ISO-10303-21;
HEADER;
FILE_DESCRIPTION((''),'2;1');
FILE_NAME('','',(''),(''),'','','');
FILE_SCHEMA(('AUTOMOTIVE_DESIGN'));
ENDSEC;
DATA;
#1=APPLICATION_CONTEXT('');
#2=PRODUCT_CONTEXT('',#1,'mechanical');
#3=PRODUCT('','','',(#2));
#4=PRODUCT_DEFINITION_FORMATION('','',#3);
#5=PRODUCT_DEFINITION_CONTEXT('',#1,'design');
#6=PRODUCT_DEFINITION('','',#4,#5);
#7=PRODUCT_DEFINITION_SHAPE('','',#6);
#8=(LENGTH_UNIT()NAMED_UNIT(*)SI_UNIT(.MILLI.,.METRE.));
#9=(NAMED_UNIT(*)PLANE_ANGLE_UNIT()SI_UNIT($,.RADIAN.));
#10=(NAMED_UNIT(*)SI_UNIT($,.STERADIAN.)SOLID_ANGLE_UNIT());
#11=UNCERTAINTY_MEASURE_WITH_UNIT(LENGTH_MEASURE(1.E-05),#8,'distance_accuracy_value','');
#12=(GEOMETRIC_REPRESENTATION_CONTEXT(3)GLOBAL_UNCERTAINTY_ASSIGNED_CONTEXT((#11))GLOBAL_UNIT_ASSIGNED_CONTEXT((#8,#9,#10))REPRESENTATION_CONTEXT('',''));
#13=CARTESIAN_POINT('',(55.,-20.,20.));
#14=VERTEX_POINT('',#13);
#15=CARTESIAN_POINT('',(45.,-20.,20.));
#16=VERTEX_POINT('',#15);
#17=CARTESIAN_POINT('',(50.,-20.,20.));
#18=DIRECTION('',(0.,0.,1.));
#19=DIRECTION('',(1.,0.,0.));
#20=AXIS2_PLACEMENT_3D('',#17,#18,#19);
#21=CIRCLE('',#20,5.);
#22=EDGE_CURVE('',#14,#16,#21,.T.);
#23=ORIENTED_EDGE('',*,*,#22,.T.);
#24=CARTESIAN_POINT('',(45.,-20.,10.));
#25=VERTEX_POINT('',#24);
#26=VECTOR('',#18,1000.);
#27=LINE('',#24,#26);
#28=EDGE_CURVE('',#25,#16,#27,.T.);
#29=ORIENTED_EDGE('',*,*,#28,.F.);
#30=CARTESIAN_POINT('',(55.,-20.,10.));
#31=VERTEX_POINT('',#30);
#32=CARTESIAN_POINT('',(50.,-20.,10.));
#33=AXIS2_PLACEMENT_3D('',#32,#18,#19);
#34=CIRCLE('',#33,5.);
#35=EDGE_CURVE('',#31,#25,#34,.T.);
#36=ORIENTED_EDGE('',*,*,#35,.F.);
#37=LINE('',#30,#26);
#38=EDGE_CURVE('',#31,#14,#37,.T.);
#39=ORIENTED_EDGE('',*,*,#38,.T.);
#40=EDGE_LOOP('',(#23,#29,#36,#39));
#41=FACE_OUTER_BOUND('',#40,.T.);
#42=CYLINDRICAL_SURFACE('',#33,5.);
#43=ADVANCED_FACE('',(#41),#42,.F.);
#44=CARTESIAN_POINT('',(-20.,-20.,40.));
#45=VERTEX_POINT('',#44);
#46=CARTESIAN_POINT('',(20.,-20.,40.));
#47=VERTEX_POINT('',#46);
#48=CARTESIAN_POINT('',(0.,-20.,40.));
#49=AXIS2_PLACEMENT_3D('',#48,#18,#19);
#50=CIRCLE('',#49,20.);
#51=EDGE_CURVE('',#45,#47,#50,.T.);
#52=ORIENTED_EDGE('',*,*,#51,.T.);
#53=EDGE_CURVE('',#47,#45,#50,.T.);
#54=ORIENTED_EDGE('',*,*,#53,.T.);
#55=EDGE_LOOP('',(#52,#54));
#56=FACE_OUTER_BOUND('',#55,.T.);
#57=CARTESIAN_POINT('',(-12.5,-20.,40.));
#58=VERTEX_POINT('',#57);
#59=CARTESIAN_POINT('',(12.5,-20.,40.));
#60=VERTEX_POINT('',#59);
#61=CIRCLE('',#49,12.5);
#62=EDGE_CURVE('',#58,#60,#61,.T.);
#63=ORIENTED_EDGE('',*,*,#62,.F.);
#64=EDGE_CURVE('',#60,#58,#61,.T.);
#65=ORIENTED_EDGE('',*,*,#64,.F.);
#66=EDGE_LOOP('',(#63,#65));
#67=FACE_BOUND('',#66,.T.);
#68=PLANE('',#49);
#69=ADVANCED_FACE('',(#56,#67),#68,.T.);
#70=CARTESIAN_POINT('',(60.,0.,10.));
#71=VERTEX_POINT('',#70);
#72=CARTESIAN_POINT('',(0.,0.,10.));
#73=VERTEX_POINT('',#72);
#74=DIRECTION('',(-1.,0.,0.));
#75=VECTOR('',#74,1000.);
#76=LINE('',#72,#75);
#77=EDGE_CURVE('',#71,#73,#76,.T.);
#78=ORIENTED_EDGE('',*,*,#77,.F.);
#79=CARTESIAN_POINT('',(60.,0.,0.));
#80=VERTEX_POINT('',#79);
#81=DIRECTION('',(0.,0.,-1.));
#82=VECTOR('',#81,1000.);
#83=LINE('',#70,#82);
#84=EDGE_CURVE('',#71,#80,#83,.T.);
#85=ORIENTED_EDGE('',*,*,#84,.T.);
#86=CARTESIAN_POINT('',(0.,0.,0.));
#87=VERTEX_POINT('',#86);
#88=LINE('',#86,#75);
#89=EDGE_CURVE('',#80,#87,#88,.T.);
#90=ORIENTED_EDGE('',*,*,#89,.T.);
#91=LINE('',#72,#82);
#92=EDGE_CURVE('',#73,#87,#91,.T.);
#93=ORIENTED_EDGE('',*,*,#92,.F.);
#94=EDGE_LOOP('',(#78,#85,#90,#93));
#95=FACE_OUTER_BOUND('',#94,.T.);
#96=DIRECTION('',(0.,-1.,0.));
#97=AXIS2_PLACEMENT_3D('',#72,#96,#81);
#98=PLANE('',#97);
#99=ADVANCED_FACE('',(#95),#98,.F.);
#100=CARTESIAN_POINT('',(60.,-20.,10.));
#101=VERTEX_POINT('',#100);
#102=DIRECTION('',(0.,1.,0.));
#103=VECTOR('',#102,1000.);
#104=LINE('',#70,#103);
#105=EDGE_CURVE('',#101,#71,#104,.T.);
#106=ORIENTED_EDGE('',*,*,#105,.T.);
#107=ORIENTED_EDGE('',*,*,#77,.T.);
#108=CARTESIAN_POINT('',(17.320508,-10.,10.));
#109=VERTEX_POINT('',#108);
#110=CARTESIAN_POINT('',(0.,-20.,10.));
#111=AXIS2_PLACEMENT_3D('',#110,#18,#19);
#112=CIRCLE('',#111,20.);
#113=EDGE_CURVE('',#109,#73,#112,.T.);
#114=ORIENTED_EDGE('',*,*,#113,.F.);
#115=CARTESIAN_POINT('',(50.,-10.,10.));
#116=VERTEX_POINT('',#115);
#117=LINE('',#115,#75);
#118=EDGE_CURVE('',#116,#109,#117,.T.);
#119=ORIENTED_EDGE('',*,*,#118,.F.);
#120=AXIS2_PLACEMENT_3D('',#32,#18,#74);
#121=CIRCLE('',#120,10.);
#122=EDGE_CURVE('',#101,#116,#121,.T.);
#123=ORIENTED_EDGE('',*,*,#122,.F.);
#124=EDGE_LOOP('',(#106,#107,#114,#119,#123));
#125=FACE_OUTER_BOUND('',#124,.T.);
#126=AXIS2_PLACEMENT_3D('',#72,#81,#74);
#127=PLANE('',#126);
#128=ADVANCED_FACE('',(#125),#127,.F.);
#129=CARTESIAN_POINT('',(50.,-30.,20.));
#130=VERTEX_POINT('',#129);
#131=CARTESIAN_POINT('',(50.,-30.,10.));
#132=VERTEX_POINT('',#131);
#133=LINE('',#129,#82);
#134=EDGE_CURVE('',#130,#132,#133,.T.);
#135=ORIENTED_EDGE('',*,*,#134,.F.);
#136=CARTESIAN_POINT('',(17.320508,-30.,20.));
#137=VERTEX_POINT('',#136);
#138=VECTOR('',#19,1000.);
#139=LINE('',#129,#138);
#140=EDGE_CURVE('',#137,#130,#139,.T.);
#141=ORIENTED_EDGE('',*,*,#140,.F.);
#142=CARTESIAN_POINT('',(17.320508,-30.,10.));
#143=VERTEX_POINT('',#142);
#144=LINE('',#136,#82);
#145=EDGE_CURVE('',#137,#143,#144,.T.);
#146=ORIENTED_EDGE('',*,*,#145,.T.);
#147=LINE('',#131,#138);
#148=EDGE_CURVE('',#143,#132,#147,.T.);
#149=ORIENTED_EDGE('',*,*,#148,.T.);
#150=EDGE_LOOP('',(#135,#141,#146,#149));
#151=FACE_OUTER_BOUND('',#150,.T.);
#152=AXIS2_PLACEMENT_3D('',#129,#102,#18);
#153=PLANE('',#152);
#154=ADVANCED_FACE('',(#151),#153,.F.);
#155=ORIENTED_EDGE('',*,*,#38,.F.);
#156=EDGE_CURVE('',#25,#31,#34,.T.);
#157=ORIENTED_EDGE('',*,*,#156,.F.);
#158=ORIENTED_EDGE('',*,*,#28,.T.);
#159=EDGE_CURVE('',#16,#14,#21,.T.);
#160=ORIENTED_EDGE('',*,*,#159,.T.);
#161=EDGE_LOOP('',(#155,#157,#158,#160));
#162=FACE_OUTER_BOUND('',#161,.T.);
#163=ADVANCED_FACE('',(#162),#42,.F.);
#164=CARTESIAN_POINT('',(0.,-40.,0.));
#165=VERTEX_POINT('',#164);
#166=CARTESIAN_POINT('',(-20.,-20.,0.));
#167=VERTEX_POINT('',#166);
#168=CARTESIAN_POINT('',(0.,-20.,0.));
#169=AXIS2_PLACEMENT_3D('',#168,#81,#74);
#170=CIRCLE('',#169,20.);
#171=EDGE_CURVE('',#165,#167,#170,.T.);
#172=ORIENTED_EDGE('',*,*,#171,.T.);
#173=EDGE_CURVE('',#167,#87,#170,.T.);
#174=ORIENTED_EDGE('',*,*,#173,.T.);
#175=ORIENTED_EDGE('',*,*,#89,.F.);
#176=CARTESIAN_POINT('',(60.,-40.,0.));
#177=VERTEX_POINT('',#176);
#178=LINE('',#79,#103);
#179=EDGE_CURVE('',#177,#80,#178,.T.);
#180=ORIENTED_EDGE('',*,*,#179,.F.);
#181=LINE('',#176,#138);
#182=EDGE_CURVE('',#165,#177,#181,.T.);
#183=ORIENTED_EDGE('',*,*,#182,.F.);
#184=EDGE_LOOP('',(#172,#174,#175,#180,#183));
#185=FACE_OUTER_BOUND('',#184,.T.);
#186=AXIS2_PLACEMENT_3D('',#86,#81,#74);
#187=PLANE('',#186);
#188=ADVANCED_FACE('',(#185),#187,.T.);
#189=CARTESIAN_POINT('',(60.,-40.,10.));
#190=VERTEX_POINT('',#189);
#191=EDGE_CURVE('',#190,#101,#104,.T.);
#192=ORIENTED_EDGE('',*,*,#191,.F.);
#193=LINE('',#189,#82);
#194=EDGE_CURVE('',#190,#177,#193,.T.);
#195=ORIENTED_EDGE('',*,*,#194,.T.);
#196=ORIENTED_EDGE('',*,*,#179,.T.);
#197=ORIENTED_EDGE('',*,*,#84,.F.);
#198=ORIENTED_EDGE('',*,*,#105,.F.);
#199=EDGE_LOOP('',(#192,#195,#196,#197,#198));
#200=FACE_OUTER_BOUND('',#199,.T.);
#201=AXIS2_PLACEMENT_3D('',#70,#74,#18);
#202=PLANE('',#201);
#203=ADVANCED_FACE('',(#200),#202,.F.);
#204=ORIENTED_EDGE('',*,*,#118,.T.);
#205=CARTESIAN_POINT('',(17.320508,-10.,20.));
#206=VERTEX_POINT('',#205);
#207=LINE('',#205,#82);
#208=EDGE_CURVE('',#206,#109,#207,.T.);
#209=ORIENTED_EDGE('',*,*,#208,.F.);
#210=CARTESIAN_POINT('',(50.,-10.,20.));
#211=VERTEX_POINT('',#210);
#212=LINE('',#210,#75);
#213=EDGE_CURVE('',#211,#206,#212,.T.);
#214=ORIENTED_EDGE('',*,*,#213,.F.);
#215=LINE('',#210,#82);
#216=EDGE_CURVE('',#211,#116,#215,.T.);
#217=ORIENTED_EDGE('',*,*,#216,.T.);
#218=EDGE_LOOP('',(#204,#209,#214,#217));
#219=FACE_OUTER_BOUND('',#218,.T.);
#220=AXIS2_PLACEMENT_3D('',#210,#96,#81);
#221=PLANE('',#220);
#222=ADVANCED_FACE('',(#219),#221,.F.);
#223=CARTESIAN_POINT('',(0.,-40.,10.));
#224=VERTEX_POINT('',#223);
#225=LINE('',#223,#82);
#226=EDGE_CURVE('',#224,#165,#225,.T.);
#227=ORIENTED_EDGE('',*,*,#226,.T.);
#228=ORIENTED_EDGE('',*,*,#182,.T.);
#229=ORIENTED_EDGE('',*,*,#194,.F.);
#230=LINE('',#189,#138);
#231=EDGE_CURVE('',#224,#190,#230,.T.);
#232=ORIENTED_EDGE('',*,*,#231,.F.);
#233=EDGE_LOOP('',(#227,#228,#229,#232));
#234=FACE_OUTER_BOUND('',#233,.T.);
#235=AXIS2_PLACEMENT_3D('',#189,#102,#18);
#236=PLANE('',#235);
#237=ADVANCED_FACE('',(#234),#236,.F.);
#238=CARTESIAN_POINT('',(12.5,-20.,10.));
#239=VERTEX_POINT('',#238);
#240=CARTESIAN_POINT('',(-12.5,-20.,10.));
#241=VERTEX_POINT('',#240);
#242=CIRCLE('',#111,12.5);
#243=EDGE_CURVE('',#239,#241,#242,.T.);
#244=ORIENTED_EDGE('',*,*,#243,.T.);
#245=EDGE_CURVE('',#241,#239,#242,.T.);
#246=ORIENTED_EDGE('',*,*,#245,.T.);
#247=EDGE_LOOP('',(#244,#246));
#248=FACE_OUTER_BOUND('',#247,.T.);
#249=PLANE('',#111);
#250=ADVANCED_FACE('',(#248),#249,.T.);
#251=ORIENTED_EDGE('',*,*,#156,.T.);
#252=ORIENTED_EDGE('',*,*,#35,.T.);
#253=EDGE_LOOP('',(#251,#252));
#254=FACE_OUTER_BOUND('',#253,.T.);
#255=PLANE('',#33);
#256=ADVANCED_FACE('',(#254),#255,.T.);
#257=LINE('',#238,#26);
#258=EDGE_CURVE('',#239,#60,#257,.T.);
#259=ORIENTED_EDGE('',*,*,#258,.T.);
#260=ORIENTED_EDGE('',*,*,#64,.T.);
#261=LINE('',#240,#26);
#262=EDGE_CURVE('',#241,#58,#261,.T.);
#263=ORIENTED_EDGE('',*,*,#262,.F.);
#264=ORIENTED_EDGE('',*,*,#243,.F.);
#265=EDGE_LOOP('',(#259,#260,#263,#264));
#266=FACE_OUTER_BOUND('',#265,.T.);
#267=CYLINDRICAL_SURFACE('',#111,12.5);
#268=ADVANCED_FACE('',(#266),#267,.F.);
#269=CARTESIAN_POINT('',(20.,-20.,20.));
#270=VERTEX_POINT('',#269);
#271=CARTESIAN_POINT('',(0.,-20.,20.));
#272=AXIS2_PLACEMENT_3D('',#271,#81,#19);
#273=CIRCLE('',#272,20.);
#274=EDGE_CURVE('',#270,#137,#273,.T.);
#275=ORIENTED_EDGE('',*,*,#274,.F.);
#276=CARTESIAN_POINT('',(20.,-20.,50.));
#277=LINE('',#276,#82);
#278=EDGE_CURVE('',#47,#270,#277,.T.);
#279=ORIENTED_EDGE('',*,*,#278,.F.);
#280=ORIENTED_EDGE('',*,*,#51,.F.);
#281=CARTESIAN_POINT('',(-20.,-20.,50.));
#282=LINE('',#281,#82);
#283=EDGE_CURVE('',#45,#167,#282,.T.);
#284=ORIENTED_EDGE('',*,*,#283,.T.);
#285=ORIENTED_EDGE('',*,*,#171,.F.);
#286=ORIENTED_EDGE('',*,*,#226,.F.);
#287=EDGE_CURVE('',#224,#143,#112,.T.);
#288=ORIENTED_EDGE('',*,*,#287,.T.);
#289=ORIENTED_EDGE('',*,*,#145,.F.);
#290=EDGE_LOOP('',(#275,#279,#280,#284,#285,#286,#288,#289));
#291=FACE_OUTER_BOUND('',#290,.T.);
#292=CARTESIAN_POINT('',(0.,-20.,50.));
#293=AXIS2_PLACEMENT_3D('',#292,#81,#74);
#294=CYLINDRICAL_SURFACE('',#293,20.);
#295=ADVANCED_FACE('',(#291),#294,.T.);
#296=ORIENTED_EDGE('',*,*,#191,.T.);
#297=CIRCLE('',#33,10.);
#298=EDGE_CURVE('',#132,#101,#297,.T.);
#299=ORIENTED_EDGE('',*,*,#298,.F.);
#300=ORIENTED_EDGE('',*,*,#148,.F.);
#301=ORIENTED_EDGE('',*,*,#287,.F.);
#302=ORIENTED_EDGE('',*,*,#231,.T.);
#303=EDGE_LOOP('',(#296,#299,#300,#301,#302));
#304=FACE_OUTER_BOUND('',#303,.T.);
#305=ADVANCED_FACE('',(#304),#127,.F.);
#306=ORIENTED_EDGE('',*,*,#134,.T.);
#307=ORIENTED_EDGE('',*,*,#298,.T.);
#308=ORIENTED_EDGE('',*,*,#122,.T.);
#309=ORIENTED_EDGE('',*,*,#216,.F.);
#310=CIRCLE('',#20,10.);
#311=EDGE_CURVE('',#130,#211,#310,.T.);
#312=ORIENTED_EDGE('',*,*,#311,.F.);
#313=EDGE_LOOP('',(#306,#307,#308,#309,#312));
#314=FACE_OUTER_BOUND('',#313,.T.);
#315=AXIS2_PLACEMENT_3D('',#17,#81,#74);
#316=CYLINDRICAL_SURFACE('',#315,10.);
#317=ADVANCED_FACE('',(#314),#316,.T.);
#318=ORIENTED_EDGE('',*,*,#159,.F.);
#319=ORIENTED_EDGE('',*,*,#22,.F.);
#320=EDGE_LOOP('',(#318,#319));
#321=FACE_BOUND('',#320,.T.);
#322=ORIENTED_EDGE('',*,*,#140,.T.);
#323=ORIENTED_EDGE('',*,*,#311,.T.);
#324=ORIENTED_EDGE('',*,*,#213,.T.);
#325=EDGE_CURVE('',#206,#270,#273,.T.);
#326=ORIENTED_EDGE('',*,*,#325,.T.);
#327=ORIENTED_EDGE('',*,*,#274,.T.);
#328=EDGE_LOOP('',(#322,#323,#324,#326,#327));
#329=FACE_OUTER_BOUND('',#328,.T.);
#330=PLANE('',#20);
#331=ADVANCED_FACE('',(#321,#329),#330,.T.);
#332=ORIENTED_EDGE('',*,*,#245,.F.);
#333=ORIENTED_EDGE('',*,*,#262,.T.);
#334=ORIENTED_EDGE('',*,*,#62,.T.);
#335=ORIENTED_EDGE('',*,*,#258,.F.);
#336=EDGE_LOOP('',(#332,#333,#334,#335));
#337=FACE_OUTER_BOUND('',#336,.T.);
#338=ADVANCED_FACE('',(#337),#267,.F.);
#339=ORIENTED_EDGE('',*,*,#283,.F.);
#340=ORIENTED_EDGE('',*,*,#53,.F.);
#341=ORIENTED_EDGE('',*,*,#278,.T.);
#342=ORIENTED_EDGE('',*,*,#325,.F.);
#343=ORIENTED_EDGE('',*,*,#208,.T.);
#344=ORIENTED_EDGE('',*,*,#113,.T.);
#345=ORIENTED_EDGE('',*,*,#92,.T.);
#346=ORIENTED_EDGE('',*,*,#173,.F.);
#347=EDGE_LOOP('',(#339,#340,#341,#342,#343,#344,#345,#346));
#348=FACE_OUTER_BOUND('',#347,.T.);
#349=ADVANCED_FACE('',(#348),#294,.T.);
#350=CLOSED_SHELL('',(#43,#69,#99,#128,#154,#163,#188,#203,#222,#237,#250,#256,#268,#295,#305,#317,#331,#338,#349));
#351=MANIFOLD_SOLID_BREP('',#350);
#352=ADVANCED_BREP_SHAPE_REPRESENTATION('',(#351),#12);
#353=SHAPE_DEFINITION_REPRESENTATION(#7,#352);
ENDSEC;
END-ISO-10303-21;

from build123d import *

# Parameters (mm, degrees)
BASE_PLATE_SKETCH_W                = 60
BASE_PLATE_SKETCH_H                = 40
BASE_PLATE_DEPTH                   = 10
CYLINDER_BOSS_SKETCH_40_R          = 20
CYLINDER_BOSS_40_DEPTH             = 40
CYLINDER_ROOT_BOSS_SKETCH_40_R     = 20
CYLINDER_ROOT_BOSS_40_DEPTH        = 10
CYLINDER_START                     = -10
CYLINDER_CLEARANCE_CUT_SKETCH_40_R = 20
CYLINDER_CLEARANCE_CUT_40_DEPTH    = 10
LUG_ARM_DEPTH                      = 10
LUG_HOLE_SKETCH_10_R               = 5
LUG_HOLE_10_DEPTH                  = 10
BORE_SKETCH_25_R                   = 12.5
BORE_25_DEPTH                      = 30


with BuildPart() as part:
    # Base Plate Sketch → Base Plate (new body)
    with BuildSketch(Plane.XY):
        with Locations((30, -20)):
            Rectangle(BASE_PLATE_SKETCH_W, BASE_PLATE_SKETCH_H)
    extrude(amount=BASE_PLATE_DEPTH)

    # Cylinder Boss Sketch Ø40 → Cylinder Boss Ø40 (add)
    with BuildSketch(Plane.XY.offset(10)):
        with Locations(Location((0, -20, 0), (0, 0, 270))):
            Circle(CYLINDER_BOSS_SKETCH_40_R)
    extrude(amount=CYLINDER_BOSS_40_DEPTH)

    # Cylinder Root Boss Sketch Ø40 → Cylinder Root Boss Ø40 (add)
    with BuildSketch(Plane(origin=(0, 0, 0), x_dir=(-1, 0, 0), z_dir=(0, 0, -1))):
        with Locations(Location((0, -20, 0), (0, 0, 90))):
            Circle(CYLINDER_ROOT_BOSS_SKETCH_40_R)
    extrude(amount=-CYLINDER_ROOT_BOSS_40_DEPTH)

    # Cylinder Clearance Cut Sketch Ø40 → Cylinder Clearance Cut Ø40 (cut)
    with BuildSketch(Plane.XY.offset(50).offset(CYLINDER_START)):
        with Locations(Location((0, -20, 0), (0, 0, 90))):
            Circle(CYLINDER_CLEARANCE_CUT_SKETCH_40_R)
    extrude(amount=CYLINDER_CLEARANCE_CUT_40_DEPTH, mode=Mode.SUBTRACT)

    # Lug Arm Sketch → Lug Arm (add)
    with BuildSketch(Plane.XY.offset(10)):
        with BuildLine():
            Line((50, -10), (17.320508076, -10))
            ThreePointArc((17.320508076, -10), (20, -20), (17.320508076, -30))
            Line((17.320508076, -30), (50, -30))
            ThreePointArc((50, -30), (60, -20), (50, -10))
        make_face()
    extrude(amount=LUG_ARM_DEPTH)

    # Lug Hole Sketch Ø10 → Lug Hole Ø10 (cut)
    with BuildSketch(Plane.XY.offset(20)):
        with Locations((50, -20)):
            Circle(LUG_HOLE_SKETCH_10_R)
    extrude(amount=-LUG_HOLE_10_DEPTH, mode=Mode.SUBTRACT)

    # Bore Sketch Ø25 → Bore Ø25 (cut)
    with BuildSketch(Plane.XY.offset(40)):
        with Locations((0, -20)):
            Circle(BORE_SKETCH_25_R)
    extrude(amount=-BORE_25_DEPTH, mode=Mode.SUBTRACT)


solid = part.part
